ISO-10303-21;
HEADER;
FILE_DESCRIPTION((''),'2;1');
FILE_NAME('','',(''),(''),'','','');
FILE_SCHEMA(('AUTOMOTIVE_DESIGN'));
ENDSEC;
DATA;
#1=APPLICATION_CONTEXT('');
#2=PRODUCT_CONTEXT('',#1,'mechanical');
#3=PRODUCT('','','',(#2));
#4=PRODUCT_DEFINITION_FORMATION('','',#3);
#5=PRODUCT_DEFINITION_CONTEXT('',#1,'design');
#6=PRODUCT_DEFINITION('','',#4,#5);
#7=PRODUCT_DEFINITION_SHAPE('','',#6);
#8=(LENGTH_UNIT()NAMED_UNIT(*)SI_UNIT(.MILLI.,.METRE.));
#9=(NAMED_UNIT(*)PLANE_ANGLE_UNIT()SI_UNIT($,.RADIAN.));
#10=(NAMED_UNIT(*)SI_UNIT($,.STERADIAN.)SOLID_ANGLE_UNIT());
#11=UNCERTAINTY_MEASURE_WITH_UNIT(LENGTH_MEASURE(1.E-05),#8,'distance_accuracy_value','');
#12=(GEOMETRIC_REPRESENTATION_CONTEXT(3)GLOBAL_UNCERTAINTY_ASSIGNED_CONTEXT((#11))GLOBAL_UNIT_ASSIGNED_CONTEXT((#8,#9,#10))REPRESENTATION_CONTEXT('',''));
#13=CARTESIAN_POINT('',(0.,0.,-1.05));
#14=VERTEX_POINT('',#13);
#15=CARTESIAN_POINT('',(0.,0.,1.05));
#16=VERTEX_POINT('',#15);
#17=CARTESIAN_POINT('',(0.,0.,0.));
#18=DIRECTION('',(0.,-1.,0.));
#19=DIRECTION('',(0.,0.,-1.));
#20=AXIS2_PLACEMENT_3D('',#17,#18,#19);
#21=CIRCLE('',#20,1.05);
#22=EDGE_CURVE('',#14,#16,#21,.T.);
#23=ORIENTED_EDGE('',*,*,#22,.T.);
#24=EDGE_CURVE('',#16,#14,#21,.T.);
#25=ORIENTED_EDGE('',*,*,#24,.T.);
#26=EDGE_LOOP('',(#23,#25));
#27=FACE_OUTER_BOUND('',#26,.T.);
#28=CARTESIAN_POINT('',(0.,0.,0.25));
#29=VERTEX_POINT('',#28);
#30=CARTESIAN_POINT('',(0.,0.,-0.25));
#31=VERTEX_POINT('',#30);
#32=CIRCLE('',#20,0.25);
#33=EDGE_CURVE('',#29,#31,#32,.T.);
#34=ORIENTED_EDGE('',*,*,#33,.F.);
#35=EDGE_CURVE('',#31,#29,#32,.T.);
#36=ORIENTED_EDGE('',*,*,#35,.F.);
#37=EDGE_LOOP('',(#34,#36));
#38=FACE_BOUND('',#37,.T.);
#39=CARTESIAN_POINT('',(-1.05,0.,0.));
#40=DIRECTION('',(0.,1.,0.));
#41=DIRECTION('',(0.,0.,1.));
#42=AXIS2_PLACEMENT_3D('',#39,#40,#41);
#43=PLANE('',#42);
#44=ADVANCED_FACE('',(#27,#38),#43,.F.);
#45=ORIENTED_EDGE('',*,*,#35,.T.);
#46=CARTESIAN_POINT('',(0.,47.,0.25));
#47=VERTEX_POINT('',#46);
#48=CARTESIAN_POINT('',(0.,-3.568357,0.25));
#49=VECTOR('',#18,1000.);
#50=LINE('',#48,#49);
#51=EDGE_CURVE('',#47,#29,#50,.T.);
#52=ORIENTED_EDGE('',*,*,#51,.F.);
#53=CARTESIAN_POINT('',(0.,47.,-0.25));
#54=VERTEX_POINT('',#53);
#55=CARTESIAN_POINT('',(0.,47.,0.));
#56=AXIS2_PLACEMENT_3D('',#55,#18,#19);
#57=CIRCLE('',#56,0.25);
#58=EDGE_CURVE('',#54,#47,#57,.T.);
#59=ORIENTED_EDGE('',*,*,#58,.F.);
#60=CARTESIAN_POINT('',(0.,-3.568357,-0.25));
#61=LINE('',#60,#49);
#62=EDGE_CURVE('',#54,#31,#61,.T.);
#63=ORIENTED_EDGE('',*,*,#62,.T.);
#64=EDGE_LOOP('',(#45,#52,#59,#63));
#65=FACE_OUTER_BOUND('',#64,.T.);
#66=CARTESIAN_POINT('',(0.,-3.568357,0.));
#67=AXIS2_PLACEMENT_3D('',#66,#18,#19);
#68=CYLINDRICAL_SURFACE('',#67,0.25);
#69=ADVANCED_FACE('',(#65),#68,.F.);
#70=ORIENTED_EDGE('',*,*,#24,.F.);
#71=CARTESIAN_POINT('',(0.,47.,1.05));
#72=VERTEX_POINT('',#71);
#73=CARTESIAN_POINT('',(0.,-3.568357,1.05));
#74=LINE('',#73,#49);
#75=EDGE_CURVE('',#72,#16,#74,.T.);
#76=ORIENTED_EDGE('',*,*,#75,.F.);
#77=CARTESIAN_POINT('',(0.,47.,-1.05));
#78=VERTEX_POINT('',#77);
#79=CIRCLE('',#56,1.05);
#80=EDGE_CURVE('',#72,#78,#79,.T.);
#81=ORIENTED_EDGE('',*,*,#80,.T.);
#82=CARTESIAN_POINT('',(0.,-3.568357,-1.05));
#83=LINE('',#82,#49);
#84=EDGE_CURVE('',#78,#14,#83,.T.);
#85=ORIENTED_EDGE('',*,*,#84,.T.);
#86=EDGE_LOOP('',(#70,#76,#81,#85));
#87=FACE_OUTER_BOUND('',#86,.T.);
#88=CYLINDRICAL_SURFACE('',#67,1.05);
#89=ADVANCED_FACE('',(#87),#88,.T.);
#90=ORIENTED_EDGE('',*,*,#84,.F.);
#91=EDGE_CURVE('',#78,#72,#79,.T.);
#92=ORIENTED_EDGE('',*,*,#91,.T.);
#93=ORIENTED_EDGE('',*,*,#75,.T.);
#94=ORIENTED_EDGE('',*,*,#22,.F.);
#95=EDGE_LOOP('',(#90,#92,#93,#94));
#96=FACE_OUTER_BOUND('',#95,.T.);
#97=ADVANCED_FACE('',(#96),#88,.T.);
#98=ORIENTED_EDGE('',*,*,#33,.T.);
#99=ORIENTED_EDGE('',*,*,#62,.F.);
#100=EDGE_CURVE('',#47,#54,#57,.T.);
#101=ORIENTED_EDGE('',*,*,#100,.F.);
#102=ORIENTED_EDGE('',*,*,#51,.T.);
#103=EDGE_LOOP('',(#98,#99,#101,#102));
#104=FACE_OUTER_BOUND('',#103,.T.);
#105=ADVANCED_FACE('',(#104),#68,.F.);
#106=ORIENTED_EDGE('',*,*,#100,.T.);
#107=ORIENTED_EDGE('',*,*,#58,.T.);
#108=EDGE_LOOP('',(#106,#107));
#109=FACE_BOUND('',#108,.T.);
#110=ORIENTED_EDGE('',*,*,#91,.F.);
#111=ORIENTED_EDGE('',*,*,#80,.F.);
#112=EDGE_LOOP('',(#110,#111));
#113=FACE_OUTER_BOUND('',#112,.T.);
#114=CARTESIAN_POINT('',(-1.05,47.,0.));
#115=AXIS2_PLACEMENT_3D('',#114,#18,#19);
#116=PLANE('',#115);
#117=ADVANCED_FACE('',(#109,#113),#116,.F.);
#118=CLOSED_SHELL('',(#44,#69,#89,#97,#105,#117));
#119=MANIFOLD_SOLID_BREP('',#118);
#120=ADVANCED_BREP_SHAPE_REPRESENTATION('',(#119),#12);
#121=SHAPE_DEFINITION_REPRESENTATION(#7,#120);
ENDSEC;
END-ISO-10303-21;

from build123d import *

# Parameters (mm, degrees)
SKETCH1_W = 0.8
SKETCH1_H = 47


with BuildPart() as part:
    # Sketch1 → Revolve1 (revolve)
    with BuildSketch(Plane.XY, mode=Mode.PRIVATE) as revolve1_sk:
        with Locations((-0.65, 23.5)):
            Rectangle(SKETCH1_W, SKETCH1_H)
    revolve(revolve1_sk.sketch.rotate(Axis((0, -3.568356633, 0), (0, 1, 0)), 270), axis=Axis((0, -3.568356633, 0), (0, 1, 0)))


solid = part.part
